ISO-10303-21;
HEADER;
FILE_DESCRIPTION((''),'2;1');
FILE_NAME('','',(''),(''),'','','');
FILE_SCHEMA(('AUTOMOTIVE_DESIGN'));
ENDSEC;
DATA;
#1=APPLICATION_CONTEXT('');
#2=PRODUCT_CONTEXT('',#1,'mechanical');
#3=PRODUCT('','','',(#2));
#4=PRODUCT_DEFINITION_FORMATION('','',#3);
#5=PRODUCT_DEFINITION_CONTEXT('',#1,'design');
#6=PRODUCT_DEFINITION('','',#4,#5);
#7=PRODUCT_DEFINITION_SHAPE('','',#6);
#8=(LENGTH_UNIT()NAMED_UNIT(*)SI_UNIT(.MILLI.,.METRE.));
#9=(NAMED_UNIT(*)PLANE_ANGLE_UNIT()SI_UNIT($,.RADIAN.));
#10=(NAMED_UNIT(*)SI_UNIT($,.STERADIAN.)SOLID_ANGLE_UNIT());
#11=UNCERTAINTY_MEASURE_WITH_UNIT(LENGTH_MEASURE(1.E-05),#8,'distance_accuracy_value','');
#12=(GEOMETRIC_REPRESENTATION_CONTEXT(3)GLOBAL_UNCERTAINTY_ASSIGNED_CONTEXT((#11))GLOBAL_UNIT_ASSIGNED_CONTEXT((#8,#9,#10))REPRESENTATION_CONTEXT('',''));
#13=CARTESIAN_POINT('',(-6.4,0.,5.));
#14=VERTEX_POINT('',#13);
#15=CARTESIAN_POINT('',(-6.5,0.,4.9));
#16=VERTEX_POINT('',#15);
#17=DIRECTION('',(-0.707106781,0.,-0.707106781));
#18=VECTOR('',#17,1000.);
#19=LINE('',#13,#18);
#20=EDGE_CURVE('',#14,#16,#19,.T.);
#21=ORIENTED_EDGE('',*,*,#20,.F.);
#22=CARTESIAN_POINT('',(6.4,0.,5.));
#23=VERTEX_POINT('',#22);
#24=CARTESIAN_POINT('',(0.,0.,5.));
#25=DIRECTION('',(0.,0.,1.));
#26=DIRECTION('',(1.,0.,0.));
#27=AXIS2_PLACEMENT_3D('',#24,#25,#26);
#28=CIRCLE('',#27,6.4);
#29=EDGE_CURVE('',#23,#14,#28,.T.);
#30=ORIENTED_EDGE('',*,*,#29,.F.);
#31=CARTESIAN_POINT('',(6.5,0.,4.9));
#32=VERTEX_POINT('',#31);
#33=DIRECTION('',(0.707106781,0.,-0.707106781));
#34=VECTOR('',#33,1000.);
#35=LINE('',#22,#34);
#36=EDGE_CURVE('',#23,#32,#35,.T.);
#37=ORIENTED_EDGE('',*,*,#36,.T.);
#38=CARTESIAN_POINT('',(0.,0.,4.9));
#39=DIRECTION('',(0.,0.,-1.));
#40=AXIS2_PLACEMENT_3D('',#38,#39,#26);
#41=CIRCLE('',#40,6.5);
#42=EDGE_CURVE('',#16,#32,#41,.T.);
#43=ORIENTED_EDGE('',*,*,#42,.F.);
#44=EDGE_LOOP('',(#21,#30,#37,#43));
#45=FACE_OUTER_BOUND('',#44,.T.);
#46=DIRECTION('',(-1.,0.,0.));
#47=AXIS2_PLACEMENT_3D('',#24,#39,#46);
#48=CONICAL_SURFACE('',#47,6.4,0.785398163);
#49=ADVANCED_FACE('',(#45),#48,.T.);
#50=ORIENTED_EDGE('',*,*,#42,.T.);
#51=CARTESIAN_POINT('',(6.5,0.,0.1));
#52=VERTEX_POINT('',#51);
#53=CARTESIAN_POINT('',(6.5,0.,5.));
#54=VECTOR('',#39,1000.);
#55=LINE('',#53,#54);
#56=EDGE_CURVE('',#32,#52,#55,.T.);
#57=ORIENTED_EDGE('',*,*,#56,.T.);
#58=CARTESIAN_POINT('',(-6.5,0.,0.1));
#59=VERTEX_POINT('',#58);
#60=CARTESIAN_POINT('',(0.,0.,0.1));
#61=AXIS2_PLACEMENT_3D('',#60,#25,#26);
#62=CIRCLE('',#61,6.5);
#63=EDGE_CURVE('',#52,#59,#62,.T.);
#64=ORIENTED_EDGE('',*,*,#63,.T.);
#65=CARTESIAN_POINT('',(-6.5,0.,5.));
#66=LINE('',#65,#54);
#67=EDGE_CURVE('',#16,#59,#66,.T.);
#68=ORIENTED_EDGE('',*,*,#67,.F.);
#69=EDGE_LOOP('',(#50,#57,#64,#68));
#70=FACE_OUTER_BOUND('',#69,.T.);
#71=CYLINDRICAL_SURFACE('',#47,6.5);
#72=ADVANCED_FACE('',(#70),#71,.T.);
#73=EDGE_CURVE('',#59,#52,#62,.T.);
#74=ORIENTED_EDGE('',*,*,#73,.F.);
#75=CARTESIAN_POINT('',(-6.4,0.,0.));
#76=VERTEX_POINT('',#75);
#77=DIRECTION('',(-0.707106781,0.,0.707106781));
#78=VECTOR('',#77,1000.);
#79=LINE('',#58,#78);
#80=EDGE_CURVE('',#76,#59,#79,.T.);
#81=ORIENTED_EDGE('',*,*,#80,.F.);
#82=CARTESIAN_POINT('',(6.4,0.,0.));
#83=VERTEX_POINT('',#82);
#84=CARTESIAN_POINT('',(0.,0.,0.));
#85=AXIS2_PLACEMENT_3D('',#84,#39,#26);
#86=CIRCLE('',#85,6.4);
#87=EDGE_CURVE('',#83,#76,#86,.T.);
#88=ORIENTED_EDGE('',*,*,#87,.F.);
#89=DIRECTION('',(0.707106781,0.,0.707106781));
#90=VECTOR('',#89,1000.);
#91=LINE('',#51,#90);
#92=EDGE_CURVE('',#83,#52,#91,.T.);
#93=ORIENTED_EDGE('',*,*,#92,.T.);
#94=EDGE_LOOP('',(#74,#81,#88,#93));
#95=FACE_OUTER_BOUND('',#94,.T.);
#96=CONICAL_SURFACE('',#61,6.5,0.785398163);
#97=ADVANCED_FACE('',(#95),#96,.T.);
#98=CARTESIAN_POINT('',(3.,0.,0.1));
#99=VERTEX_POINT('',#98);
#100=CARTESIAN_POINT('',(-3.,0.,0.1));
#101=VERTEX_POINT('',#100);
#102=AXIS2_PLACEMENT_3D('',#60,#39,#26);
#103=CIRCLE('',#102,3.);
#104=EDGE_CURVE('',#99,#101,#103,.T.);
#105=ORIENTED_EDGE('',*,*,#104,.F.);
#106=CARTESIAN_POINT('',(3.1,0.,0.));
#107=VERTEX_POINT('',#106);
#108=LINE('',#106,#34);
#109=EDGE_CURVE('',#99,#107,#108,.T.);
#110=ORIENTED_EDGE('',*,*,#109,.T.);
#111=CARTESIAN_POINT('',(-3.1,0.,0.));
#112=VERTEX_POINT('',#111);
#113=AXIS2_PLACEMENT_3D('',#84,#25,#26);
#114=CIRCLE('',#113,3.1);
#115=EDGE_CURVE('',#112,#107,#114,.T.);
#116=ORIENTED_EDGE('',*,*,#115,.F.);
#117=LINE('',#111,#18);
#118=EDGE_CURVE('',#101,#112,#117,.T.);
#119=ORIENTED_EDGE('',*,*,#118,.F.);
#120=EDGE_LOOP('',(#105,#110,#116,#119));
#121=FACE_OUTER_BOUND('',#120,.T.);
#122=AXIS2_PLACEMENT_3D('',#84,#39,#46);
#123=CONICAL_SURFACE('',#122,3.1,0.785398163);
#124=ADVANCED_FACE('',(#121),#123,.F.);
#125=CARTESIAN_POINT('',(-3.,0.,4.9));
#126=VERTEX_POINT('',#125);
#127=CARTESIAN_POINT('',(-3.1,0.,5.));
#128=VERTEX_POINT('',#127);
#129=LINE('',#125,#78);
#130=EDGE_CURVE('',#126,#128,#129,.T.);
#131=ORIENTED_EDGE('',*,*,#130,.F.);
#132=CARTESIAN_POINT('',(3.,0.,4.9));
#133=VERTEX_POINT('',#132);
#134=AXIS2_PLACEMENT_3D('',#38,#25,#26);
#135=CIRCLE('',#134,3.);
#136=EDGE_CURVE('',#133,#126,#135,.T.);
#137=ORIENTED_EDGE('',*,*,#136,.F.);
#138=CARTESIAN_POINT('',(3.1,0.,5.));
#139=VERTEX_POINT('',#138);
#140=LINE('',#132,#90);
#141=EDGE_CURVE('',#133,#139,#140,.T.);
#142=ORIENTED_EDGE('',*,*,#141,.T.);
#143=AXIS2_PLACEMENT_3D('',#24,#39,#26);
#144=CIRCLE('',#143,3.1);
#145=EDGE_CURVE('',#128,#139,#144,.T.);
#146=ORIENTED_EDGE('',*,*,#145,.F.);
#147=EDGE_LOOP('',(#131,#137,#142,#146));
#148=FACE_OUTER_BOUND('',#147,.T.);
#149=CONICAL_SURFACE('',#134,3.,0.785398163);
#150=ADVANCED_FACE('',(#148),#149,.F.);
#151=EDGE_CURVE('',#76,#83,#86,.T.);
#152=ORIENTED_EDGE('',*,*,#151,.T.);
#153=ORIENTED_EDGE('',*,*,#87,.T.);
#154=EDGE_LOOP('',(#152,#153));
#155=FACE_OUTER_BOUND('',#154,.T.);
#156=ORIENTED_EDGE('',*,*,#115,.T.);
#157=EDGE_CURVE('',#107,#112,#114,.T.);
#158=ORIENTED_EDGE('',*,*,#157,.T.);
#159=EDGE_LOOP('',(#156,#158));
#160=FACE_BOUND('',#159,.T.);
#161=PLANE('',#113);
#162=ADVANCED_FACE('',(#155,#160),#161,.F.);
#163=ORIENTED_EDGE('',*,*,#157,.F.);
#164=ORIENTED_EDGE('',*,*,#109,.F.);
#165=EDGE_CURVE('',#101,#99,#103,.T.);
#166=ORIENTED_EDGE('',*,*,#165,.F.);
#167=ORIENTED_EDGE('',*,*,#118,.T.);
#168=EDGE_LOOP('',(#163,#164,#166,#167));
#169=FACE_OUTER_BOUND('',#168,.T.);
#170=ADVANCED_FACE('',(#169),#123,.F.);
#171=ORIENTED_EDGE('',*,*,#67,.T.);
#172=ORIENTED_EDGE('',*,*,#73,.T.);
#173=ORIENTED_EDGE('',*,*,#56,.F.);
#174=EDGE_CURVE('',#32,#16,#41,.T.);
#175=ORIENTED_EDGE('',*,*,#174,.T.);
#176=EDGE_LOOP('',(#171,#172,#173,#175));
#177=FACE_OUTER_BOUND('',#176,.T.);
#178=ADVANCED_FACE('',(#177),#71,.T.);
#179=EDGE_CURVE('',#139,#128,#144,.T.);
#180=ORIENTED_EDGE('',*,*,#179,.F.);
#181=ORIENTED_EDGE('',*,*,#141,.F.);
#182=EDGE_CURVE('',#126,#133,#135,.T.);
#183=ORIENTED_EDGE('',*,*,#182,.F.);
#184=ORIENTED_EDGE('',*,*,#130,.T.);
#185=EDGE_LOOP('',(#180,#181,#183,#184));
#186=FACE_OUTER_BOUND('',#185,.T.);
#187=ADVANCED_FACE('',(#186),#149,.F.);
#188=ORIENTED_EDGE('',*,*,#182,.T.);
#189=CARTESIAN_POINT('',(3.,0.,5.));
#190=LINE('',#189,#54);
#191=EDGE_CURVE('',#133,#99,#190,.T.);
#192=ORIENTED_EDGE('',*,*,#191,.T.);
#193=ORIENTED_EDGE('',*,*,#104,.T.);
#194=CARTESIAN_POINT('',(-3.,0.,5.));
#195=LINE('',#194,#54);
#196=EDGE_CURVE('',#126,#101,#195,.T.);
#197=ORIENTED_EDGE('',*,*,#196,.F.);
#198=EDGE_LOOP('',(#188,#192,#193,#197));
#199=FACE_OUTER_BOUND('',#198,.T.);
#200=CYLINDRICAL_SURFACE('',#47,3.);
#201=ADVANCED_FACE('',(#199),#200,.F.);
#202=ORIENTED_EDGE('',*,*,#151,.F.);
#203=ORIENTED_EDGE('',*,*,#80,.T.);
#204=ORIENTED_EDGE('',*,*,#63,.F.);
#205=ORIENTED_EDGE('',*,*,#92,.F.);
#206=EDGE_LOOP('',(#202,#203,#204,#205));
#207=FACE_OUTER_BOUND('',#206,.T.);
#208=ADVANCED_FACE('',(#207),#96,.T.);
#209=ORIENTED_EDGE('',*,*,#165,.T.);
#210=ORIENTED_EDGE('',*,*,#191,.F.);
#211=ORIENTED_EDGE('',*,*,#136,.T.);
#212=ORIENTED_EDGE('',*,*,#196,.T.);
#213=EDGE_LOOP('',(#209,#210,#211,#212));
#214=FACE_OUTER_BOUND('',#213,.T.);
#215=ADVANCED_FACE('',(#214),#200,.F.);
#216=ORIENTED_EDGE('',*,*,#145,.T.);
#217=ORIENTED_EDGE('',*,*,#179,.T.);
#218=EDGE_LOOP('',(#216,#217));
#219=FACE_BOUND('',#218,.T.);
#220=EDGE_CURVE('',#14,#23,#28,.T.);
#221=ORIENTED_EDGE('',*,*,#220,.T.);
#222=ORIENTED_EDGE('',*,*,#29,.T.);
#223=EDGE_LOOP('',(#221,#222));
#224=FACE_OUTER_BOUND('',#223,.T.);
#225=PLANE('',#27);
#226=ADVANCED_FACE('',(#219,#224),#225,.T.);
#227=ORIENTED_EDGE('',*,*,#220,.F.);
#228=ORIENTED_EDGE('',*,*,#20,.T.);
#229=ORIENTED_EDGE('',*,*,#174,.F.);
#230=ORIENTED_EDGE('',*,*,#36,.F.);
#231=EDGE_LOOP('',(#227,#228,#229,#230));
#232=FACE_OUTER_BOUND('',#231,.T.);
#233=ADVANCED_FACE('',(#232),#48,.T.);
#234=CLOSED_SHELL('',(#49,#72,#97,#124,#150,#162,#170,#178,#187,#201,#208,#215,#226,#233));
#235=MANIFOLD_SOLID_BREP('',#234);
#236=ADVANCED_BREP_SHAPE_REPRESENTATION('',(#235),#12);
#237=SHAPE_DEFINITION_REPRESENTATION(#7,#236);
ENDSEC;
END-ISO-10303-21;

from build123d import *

# Parameters (mm, degrees)
SKETCH1_R           = 6.5
SKETCH1_R_2         = 3
BOSS_EXTRUDE1_DEPTH = 5
CHAMFER1_SIZE       = 0.1


with BuildPart() as part:
    # Sketch1 → Boss-Extrude1 (new body)
    with BuildSketch(Plane.XY):
        Circle(SKETCH1_R)
        Circle(SKETCH1_R_2, mode=Mode.SUBTRACT)
    extrude(amount=BOSS_EXTRUDE1_DEPTH)

    # Chamfer1
    chamfer1_edges = [part.edges().sort_by_distance(p)[0] for p in [
        (-6.5, 0, 0),
        (-6.5, 0, 5),
        (-3, 0, 0),
        (-3, 0, 5),
    ]]
    chamfer(chamfer1_edges, length=CHAMFER1_SIZE)


solid = part.part
